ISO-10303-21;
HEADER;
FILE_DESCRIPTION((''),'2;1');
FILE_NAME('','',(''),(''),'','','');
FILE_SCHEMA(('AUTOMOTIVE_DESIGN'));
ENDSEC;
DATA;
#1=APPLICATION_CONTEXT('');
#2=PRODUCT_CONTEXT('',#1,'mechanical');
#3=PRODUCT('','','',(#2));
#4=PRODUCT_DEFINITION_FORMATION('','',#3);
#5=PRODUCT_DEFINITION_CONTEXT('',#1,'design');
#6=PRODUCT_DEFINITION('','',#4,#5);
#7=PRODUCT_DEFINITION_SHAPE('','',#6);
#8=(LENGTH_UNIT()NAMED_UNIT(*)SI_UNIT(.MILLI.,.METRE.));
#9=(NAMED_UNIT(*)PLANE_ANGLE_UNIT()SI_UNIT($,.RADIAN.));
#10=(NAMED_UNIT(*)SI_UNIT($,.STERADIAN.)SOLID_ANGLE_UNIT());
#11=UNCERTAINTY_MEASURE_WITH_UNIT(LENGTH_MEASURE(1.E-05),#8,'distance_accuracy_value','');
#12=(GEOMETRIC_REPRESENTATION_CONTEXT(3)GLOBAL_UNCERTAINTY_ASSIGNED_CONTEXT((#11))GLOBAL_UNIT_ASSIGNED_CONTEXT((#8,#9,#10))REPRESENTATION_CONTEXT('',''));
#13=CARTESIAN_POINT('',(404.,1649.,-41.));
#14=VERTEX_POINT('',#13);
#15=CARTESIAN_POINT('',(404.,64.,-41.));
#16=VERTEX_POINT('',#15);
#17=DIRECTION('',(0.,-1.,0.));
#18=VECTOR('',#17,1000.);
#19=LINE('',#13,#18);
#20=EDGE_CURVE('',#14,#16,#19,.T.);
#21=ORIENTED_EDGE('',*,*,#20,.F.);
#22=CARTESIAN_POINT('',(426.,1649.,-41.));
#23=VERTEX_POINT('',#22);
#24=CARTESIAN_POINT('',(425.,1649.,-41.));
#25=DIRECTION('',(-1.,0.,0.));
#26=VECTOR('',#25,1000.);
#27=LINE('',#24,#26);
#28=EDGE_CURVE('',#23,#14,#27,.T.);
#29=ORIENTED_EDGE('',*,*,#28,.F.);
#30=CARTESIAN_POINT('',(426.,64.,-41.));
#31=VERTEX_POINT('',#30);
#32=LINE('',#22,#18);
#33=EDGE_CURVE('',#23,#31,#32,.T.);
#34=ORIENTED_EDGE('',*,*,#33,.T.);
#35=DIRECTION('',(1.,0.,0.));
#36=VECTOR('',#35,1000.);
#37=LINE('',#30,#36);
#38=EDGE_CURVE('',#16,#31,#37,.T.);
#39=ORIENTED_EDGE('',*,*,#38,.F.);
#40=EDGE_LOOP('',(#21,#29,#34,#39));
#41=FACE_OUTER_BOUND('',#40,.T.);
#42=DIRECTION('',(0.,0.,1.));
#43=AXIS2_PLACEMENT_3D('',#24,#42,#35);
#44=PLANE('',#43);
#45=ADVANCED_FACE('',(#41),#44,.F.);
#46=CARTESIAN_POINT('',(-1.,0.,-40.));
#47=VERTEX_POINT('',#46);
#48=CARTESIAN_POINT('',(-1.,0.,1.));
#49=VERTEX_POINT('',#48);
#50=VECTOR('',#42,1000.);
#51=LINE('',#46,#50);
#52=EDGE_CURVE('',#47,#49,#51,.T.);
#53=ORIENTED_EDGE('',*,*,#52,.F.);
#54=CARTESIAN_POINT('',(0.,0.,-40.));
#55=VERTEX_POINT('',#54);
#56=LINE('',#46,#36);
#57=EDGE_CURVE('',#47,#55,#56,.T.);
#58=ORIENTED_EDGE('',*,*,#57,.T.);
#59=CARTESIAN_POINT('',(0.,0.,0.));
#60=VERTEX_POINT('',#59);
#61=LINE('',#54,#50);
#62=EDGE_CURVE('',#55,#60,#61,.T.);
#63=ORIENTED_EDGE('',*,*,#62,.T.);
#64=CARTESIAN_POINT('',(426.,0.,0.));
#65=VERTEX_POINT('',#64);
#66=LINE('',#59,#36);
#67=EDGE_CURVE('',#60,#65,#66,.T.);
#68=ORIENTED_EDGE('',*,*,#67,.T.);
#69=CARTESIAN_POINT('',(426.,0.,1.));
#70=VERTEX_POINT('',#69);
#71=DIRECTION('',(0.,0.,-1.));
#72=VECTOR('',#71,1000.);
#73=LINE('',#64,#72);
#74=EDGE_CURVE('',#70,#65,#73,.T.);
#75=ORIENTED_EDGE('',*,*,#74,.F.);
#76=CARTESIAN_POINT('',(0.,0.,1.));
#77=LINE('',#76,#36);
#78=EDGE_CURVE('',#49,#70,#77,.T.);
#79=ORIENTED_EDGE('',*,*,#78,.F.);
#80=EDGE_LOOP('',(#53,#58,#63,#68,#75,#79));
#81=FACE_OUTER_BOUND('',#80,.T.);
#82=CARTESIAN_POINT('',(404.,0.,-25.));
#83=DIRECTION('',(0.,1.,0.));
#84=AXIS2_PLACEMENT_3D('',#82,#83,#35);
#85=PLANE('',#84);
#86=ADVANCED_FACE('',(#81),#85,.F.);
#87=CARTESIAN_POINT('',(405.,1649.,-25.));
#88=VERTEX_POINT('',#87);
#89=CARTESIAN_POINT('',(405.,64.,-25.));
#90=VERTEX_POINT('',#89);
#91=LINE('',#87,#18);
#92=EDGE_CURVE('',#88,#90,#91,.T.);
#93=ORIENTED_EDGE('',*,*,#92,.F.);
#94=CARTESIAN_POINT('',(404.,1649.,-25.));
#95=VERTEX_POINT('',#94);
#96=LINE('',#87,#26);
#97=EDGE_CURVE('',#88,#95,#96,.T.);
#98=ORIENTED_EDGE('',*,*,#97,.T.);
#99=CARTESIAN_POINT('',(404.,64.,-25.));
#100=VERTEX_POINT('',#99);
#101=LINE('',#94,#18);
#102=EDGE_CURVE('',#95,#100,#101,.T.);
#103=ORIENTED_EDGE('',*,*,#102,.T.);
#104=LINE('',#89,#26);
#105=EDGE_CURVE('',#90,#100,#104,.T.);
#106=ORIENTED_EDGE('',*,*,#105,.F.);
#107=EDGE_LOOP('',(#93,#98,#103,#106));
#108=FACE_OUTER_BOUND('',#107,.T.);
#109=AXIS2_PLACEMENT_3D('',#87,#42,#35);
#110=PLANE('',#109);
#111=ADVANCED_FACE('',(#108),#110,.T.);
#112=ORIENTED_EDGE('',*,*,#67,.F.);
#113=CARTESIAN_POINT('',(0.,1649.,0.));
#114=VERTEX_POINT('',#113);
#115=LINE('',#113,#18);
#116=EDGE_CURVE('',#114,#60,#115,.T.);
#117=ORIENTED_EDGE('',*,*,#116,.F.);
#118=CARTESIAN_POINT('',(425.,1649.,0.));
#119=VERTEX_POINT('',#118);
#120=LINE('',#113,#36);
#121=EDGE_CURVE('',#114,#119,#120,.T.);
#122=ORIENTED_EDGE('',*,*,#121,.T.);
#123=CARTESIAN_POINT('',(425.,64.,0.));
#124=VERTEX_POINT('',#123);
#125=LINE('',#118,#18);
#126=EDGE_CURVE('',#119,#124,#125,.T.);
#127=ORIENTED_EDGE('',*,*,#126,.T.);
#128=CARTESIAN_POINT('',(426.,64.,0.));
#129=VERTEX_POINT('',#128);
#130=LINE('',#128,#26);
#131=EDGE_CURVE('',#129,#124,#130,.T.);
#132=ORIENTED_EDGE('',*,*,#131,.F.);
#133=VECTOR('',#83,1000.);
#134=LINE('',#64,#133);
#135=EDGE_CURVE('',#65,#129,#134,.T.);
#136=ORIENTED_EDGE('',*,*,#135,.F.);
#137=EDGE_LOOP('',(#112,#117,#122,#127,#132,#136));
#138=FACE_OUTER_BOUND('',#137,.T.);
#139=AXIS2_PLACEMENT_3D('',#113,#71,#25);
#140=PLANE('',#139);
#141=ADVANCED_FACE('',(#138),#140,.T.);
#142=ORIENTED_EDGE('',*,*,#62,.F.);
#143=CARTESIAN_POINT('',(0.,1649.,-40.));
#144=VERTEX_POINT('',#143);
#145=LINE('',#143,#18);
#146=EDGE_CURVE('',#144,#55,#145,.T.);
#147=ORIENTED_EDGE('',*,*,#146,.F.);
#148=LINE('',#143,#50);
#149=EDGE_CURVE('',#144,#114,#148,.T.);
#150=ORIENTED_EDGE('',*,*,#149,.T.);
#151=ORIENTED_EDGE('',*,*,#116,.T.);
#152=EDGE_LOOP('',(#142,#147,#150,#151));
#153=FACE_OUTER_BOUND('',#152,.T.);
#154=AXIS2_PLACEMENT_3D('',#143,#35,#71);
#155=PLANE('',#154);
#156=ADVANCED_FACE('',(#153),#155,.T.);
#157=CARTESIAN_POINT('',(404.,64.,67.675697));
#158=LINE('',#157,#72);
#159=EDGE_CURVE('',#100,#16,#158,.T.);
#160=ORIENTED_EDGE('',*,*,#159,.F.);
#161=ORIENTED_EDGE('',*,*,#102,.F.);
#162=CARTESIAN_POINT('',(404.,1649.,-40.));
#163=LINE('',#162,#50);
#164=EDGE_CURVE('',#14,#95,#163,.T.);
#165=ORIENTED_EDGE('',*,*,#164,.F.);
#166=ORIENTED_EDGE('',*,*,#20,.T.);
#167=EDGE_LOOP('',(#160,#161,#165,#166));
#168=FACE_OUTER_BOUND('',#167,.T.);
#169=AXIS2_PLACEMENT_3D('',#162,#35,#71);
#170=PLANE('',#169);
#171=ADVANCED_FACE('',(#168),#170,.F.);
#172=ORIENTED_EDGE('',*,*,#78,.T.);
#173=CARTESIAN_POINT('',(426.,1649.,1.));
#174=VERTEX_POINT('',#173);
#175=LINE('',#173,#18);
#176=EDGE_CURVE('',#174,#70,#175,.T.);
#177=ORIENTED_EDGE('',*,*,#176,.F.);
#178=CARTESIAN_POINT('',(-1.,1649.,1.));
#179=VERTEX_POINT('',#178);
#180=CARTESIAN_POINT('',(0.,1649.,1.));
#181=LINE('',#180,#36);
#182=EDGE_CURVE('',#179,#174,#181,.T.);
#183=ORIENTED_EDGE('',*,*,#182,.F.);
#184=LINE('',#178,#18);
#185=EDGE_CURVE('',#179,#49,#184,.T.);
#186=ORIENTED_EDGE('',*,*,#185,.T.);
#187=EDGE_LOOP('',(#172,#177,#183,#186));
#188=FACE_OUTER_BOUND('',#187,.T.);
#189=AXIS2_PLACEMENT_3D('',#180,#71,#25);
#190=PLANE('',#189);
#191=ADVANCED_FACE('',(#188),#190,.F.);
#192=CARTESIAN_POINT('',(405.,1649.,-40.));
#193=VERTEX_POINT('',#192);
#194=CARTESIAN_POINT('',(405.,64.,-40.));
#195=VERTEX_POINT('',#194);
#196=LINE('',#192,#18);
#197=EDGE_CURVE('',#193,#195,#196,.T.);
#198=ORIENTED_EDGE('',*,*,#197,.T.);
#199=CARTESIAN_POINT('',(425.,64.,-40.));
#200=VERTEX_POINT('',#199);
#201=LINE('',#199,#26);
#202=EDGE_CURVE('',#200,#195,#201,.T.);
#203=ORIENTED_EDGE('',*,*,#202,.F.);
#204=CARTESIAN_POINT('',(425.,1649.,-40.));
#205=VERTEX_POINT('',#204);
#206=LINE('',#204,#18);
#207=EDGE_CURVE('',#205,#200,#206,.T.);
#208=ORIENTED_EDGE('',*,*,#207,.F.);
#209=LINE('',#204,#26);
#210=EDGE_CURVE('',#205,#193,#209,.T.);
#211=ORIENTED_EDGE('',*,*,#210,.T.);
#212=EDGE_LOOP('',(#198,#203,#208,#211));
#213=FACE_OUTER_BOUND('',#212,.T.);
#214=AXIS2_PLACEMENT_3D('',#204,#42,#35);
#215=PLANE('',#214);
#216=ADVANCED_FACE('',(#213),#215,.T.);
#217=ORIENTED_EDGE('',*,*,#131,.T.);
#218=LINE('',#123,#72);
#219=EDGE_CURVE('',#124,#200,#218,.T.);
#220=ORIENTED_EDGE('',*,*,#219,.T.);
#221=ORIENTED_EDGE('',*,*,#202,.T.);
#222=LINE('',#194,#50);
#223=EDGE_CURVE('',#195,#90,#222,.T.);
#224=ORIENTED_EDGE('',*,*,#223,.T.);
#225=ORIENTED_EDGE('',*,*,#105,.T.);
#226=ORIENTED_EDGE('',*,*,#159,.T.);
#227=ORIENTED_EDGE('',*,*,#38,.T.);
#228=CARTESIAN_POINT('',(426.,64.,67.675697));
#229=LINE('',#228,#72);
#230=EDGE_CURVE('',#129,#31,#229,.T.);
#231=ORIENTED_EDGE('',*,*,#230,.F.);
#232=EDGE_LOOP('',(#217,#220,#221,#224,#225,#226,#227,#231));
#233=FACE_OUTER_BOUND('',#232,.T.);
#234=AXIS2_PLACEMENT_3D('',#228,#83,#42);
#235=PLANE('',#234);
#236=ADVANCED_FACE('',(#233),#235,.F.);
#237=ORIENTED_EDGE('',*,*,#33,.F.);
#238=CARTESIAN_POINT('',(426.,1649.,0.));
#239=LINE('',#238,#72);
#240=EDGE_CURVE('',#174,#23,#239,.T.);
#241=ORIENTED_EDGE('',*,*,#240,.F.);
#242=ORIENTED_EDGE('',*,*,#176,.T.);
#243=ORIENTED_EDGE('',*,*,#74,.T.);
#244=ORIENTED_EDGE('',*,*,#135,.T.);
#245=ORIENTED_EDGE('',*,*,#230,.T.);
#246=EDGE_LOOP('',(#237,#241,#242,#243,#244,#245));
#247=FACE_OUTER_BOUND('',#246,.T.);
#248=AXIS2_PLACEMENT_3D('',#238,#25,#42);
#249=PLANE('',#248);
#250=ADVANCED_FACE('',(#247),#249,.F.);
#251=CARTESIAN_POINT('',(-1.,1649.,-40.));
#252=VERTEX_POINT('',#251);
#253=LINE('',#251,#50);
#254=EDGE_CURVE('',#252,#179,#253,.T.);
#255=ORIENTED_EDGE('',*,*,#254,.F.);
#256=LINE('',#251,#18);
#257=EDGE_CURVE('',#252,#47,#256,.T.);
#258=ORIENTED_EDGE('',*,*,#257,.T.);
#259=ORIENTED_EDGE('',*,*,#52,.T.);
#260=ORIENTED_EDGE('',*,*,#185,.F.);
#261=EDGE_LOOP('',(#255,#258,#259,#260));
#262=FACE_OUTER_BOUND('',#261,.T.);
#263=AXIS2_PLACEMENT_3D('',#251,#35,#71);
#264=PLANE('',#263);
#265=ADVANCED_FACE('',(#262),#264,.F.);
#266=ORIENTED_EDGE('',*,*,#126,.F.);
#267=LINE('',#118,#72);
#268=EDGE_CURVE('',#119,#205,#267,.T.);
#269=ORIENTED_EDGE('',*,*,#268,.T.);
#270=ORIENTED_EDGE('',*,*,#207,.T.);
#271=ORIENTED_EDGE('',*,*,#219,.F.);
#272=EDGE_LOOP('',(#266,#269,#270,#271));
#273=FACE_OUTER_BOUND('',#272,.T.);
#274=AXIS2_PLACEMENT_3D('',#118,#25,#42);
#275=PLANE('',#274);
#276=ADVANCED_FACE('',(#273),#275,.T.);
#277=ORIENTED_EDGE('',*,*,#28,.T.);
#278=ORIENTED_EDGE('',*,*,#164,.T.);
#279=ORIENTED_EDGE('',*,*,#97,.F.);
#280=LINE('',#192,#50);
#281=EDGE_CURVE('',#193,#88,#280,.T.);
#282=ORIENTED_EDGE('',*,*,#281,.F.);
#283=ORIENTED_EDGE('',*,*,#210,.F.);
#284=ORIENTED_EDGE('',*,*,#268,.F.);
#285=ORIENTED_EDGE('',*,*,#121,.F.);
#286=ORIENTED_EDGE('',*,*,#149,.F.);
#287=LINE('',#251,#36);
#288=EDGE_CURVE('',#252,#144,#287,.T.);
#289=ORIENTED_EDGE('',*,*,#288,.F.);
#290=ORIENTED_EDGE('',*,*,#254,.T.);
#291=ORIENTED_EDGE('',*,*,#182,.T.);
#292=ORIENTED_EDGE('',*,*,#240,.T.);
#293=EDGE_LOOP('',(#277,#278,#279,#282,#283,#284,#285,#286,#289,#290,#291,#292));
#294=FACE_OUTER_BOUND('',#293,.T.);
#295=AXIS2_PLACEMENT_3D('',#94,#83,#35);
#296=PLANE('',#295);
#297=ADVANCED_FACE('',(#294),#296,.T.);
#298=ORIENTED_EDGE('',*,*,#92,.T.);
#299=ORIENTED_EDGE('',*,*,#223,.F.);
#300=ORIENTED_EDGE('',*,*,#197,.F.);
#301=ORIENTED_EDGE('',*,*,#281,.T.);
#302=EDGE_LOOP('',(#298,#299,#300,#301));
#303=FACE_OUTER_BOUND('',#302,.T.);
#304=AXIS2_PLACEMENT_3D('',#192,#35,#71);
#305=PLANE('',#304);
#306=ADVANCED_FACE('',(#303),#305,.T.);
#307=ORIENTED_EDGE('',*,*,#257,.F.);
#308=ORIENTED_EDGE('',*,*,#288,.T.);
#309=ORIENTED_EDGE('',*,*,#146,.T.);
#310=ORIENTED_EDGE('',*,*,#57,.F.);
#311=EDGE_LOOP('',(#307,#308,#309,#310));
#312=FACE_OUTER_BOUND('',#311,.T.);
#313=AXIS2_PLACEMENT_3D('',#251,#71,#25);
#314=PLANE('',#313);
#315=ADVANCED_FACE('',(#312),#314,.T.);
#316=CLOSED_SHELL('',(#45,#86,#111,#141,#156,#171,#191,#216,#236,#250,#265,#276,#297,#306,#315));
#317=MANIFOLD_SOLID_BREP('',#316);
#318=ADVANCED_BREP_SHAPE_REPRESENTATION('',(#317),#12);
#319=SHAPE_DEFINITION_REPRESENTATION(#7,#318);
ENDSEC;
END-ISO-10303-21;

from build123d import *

# Parameters (mm, degrees)
EXTRUDE_THIN1_DEPTH = 1649
SKETCH5_W           = 22
SKETCH5_H           = 64
CUT_EXTRUDE2_DEPTH  = 41


with BuildPart() as part:
    # Sketch3 → Extrude-Thin1 (new body)
    with BuildSketch(Plane(origin=(0, 0, 0), x_dir=(1, 0, 0), z_dir=(0, 1, 0))):
        Polygon((0, 40), (0, 0), (425, 0), (425, 40), (405, 40), (405, 25), (404, 25), (404, 41), (426, 41), (426, -1), (-1, -1), (-1, 40), align=None)
    extrude(amount=EXTRUDE_THIN1_DEPTH)

    # Sketch5 → Cut-Extrude2 (cut)
    with BuildSketch(Plane(origin=(0, 0, -41), x_dir=(-1, 0, 0), z_dir=(0, 0, -1))):
        with Locations((-415, 32)):
            Rectangle(SKETCH5_W, SKETCH5_H)
    extrude(amount=-CUT_EXTRUDE2_DEPTH, mode=Mode.SUBTRACT)


solid = part.part
